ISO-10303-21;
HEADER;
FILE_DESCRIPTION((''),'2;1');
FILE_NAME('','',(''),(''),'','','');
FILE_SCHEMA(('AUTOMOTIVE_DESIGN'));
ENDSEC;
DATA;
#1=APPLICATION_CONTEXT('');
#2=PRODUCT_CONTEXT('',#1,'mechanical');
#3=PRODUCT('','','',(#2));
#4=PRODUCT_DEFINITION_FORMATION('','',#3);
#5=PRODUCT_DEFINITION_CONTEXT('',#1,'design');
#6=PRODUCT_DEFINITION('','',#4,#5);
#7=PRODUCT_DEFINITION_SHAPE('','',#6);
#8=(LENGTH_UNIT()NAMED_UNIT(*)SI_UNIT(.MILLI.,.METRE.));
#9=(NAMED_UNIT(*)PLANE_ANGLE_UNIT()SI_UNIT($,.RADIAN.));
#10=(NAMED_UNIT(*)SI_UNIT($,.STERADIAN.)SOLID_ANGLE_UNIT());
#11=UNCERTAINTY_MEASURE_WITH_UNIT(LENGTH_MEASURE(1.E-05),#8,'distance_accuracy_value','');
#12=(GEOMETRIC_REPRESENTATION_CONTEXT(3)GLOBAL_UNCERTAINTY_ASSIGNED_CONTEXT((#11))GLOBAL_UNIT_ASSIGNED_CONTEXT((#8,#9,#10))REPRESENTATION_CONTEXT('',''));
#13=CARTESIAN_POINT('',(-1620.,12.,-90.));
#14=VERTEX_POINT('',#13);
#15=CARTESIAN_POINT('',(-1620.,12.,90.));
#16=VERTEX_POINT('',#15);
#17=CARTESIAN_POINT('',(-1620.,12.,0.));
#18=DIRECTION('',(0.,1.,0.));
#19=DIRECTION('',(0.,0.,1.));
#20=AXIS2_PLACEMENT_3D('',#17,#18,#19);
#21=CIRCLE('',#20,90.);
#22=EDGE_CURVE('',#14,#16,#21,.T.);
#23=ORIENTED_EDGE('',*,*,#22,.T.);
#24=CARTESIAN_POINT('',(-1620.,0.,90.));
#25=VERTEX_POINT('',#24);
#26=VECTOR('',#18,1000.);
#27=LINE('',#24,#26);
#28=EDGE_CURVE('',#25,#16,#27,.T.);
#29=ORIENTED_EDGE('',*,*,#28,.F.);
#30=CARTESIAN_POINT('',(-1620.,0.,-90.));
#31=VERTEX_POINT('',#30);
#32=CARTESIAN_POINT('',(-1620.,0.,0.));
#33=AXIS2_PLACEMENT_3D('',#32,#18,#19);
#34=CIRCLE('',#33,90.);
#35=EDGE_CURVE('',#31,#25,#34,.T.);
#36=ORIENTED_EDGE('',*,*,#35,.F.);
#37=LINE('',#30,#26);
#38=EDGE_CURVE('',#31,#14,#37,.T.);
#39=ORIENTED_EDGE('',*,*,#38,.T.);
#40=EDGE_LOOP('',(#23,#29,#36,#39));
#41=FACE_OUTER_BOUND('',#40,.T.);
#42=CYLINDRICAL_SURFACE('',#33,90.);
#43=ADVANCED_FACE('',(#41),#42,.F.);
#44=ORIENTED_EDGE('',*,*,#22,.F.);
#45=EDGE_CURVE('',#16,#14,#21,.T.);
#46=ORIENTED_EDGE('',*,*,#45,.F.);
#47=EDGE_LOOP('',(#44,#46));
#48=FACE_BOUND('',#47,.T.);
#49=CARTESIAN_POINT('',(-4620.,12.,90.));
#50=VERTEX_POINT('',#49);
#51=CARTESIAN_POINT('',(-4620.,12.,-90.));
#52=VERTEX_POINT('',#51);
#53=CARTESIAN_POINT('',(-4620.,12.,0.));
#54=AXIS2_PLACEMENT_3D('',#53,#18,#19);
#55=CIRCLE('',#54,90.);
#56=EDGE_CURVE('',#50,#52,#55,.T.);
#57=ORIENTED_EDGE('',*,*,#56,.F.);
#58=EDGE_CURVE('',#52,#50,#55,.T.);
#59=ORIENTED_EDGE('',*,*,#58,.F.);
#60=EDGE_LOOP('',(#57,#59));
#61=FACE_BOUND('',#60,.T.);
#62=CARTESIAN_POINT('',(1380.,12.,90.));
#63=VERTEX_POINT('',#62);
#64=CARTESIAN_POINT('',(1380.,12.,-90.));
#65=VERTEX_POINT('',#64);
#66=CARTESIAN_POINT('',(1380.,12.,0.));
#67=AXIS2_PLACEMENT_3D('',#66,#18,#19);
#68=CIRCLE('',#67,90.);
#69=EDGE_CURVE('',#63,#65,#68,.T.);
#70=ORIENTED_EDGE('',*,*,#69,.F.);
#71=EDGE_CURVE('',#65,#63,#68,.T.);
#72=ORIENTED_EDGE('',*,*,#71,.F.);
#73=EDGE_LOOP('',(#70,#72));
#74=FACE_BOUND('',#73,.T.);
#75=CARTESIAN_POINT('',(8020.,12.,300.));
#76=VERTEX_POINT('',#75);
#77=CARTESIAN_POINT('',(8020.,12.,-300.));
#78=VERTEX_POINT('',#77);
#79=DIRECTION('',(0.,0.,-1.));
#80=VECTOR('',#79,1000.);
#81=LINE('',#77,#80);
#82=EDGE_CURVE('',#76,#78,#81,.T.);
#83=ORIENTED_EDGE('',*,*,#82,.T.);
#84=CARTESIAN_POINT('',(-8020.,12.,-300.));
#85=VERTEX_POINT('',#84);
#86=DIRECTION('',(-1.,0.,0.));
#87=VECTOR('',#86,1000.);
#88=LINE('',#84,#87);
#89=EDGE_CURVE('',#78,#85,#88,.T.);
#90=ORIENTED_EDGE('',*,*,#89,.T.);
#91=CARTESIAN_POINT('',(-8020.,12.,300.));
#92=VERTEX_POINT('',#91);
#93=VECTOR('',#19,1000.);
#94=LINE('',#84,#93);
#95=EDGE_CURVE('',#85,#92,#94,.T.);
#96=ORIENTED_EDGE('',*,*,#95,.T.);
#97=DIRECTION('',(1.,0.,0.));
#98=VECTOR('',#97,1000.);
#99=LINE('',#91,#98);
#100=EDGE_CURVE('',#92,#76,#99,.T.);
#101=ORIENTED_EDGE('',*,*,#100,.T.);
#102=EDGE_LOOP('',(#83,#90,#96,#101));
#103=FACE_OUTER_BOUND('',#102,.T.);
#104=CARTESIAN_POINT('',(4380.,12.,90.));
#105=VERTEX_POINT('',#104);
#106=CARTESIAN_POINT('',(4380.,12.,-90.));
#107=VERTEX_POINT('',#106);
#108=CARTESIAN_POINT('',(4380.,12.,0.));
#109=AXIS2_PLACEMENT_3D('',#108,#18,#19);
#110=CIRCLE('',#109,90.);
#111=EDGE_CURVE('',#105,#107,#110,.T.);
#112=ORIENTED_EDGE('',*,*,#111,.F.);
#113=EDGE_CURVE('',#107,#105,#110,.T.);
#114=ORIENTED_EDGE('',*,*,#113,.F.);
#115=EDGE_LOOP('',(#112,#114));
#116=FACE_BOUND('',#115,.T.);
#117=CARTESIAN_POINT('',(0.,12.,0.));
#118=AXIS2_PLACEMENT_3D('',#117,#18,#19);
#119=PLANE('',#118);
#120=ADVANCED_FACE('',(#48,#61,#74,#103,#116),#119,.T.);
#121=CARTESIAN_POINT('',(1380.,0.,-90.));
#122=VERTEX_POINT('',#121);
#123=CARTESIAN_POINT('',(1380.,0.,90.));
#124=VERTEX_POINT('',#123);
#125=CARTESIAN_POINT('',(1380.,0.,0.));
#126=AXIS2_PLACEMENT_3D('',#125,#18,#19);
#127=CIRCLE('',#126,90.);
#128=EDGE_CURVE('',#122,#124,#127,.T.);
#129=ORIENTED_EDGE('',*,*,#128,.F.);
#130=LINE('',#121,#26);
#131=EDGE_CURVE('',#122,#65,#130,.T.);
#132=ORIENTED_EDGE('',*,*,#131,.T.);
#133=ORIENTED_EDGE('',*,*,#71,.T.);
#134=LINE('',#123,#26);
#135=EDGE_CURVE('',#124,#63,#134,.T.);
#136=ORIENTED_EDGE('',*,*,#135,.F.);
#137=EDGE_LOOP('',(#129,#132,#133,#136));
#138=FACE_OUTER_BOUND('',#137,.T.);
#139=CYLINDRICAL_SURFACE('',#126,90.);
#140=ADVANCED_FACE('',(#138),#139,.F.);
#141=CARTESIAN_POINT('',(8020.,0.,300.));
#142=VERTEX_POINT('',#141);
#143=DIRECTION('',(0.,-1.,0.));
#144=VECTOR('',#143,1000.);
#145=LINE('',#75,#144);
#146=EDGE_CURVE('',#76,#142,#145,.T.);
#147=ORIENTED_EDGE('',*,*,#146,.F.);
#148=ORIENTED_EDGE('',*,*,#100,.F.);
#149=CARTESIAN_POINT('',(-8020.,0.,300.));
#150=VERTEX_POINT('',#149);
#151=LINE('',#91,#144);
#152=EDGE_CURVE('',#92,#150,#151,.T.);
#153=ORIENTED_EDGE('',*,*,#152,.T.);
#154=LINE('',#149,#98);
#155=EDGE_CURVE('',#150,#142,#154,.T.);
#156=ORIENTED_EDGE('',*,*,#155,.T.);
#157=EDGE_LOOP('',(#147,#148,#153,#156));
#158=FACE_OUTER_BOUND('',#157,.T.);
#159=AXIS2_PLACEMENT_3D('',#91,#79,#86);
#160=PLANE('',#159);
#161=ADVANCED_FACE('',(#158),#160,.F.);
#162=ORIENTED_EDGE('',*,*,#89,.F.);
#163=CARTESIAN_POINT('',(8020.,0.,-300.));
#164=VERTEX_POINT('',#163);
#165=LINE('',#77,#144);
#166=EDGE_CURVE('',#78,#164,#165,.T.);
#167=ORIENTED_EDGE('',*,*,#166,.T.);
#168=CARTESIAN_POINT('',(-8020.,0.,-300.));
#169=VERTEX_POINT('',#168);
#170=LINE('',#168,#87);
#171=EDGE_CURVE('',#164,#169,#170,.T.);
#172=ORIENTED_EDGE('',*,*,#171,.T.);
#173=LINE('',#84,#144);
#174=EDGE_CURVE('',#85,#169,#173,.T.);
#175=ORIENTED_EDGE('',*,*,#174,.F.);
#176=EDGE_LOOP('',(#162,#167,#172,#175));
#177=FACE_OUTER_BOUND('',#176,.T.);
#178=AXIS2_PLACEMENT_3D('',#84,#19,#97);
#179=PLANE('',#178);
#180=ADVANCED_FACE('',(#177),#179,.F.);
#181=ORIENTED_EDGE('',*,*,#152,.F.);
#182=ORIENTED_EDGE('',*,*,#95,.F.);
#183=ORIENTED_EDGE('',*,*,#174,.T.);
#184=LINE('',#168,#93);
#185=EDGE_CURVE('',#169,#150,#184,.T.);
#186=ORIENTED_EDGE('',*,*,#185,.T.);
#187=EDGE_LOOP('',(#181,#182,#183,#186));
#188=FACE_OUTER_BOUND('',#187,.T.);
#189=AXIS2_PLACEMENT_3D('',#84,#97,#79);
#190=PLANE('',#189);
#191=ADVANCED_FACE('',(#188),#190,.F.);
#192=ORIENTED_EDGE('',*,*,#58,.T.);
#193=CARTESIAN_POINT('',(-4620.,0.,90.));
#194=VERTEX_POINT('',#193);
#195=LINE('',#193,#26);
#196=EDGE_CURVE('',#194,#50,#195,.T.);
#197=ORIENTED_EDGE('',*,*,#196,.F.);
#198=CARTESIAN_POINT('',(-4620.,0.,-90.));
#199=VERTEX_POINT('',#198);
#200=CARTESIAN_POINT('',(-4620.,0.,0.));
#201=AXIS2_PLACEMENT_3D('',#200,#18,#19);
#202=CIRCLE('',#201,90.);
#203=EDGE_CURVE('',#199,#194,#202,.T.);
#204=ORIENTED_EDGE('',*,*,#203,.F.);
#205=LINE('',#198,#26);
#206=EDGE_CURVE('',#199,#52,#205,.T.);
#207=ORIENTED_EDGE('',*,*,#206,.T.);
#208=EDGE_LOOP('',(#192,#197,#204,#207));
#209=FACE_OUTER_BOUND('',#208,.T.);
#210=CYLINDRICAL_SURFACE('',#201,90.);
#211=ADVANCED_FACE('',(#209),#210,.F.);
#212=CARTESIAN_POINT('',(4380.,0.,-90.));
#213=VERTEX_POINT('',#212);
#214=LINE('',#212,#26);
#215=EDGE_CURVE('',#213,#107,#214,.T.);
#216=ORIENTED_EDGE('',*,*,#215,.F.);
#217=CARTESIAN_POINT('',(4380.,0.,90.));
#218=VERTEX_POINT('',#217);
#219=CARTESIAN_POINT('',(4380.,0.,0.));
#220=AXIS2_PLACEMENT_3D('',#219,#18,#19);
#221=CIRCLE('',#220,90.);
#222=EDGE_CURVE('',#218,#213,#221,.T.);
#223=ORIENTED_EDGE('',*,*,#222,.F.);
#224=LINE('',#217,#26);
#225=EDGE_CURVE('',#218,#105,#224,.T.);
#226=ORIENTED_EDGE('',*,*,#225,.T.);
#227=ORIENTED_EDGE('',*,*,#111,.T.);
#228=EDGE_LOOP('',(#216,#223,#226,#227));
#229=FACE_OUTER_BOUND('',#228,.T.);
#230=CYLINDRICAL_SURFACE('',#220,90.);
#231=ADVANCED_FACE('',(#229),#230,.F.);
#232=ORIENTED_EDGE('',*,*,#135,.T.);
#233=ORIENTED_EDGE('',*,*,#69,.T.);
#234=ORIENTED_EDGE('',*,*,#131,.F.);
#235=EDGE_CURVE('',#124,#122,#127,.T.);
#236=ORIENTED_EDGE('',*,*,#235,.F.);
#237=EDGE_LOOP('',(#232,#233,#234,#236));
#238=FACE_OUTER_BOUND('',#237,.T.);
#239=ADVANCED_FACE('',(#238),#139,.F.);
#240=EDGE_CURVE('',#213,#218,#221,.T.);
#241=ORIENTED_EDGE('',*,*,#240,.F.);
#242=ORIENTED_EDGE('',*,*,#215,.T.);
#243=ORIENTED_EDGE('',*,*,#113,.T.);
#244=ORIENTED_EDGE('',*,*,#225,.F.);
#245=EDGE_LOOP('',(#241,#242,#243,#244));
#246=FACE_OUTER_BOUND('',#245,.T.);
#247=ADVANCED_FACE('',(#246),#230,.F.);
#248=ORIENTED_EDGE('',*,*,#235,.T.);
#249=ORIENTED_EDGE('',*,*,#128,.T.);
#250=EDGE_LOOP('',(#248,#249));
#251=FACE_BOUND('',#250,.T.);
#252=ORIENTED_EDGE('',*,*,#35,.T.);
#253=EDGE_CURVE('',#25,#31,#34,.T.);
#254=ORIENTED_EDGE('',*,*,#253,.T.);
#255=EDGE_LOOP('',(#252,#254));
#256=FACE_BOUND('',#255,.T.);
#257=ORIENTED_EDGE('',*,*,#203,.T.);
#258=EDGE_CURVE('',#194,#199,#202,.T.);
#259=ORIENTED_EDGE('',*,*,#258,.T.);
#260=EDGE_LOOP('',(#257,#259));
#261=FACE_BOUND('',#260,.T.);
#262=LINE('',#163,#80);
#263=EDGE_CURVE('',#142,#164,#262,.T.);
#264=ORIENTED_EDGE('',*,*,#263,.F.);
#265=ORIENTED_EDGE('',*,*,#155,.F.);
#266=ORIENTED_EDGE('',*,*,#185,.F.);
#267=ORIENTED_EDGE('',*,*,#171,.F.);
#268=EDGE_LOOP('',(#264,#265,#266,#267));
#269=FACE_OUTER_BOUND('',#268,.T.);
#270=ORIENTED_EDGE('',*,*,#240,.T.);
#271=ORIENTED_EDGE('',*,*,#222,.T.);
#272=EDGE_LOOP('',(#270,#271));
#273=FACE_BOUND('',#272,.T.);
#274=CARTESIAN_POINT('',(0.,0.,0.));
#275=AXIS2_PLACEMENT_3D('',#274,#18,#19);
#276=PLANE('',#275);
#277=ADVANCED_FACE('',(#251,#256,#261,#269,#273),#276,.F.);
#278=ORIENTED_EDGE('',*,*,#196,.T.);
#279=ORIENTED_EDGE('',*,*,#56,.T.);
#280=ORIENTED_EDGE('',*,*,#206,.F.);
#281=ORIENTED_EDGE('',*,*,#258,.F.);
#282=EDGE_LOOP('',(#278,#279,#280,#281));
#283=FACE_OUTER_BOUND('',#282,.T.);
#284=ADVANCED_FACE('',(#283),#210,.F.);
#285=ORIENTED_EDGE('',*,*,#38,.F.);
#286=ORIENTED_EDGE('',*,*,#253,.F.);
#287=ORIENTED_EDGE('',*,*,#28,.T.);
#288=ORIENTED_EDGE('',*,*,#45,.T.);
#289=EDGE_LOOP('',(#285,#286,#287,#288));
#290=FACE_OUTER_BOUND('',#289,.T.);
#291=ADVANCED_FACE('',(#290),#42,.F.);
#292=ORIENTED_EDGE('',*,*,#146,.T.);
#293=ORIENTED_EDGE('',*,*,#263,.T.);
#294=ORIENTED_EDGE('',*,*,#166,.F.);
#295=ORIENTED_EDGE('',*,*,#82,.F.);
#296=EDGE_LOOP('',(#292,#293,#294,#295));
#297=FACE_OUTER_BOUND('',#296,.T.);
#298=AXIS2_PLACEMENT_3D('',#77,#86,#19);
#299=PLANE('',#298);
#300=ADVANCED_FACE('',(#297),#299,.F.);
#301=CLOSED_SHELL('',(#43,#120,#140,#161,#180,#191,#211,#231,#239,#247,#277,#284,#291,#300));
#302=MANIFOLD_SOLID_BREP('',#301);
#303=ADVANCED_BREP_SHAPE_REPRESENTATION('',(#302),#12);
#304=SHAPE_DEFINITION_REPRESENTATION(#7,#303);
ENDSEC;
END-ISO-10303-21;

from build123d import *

# Parameters (mm, degrees)
SKETCH1_W           = 16040
SKETCH1_H           = 600
BOSS_EXTRUDE1_DEPTH = 12
SKETCH2_R           = 90
CUT_EXTRUDE1_DEPTH  = 8026.617982436
LPATTERN1_COUNT     = 4
LPATTERN1_PITCH     = 3000


with BuildPart() as part:
    # Sketch1 → Boss-Extrude1 (new body)
    with BuildSketch(Plane(origin=(0, 0, 0), x_dir=(1, 0, 0), z_dir=(0, 1, 0))):
        Rectangle(SKETCH1_W, SKETCH1_H)
    extrude(amount=BOSS_EXTRUDE1_DEPTH)

    # Sketch2 → Cut-Extrude1 (cut, through all)
    with BuildSketch(Plane(origin=(0, 12, 0), x_dir=(1, 0, 0), z_dir=(0, 1, 0))):
        with Locations(Location((-4620, 0, 0), (0, 0, 270))):
            Circle(SKETCH2_R)
    cut_extrude1 = extrude(amount=-CUT_EXTRUDE1_DEPTH, mode=Mode.SUBTRACT)

    # LPattern1: Cut-Extrude1 ×4
    with Locations(*[(i * LPATTERN1_PITCH, 0, 0) for i in range(1, LPATTERN1_COUNT)]):
        add(cut_extrude1, mode=Mode.SUBTRACT)


solid = part.part
